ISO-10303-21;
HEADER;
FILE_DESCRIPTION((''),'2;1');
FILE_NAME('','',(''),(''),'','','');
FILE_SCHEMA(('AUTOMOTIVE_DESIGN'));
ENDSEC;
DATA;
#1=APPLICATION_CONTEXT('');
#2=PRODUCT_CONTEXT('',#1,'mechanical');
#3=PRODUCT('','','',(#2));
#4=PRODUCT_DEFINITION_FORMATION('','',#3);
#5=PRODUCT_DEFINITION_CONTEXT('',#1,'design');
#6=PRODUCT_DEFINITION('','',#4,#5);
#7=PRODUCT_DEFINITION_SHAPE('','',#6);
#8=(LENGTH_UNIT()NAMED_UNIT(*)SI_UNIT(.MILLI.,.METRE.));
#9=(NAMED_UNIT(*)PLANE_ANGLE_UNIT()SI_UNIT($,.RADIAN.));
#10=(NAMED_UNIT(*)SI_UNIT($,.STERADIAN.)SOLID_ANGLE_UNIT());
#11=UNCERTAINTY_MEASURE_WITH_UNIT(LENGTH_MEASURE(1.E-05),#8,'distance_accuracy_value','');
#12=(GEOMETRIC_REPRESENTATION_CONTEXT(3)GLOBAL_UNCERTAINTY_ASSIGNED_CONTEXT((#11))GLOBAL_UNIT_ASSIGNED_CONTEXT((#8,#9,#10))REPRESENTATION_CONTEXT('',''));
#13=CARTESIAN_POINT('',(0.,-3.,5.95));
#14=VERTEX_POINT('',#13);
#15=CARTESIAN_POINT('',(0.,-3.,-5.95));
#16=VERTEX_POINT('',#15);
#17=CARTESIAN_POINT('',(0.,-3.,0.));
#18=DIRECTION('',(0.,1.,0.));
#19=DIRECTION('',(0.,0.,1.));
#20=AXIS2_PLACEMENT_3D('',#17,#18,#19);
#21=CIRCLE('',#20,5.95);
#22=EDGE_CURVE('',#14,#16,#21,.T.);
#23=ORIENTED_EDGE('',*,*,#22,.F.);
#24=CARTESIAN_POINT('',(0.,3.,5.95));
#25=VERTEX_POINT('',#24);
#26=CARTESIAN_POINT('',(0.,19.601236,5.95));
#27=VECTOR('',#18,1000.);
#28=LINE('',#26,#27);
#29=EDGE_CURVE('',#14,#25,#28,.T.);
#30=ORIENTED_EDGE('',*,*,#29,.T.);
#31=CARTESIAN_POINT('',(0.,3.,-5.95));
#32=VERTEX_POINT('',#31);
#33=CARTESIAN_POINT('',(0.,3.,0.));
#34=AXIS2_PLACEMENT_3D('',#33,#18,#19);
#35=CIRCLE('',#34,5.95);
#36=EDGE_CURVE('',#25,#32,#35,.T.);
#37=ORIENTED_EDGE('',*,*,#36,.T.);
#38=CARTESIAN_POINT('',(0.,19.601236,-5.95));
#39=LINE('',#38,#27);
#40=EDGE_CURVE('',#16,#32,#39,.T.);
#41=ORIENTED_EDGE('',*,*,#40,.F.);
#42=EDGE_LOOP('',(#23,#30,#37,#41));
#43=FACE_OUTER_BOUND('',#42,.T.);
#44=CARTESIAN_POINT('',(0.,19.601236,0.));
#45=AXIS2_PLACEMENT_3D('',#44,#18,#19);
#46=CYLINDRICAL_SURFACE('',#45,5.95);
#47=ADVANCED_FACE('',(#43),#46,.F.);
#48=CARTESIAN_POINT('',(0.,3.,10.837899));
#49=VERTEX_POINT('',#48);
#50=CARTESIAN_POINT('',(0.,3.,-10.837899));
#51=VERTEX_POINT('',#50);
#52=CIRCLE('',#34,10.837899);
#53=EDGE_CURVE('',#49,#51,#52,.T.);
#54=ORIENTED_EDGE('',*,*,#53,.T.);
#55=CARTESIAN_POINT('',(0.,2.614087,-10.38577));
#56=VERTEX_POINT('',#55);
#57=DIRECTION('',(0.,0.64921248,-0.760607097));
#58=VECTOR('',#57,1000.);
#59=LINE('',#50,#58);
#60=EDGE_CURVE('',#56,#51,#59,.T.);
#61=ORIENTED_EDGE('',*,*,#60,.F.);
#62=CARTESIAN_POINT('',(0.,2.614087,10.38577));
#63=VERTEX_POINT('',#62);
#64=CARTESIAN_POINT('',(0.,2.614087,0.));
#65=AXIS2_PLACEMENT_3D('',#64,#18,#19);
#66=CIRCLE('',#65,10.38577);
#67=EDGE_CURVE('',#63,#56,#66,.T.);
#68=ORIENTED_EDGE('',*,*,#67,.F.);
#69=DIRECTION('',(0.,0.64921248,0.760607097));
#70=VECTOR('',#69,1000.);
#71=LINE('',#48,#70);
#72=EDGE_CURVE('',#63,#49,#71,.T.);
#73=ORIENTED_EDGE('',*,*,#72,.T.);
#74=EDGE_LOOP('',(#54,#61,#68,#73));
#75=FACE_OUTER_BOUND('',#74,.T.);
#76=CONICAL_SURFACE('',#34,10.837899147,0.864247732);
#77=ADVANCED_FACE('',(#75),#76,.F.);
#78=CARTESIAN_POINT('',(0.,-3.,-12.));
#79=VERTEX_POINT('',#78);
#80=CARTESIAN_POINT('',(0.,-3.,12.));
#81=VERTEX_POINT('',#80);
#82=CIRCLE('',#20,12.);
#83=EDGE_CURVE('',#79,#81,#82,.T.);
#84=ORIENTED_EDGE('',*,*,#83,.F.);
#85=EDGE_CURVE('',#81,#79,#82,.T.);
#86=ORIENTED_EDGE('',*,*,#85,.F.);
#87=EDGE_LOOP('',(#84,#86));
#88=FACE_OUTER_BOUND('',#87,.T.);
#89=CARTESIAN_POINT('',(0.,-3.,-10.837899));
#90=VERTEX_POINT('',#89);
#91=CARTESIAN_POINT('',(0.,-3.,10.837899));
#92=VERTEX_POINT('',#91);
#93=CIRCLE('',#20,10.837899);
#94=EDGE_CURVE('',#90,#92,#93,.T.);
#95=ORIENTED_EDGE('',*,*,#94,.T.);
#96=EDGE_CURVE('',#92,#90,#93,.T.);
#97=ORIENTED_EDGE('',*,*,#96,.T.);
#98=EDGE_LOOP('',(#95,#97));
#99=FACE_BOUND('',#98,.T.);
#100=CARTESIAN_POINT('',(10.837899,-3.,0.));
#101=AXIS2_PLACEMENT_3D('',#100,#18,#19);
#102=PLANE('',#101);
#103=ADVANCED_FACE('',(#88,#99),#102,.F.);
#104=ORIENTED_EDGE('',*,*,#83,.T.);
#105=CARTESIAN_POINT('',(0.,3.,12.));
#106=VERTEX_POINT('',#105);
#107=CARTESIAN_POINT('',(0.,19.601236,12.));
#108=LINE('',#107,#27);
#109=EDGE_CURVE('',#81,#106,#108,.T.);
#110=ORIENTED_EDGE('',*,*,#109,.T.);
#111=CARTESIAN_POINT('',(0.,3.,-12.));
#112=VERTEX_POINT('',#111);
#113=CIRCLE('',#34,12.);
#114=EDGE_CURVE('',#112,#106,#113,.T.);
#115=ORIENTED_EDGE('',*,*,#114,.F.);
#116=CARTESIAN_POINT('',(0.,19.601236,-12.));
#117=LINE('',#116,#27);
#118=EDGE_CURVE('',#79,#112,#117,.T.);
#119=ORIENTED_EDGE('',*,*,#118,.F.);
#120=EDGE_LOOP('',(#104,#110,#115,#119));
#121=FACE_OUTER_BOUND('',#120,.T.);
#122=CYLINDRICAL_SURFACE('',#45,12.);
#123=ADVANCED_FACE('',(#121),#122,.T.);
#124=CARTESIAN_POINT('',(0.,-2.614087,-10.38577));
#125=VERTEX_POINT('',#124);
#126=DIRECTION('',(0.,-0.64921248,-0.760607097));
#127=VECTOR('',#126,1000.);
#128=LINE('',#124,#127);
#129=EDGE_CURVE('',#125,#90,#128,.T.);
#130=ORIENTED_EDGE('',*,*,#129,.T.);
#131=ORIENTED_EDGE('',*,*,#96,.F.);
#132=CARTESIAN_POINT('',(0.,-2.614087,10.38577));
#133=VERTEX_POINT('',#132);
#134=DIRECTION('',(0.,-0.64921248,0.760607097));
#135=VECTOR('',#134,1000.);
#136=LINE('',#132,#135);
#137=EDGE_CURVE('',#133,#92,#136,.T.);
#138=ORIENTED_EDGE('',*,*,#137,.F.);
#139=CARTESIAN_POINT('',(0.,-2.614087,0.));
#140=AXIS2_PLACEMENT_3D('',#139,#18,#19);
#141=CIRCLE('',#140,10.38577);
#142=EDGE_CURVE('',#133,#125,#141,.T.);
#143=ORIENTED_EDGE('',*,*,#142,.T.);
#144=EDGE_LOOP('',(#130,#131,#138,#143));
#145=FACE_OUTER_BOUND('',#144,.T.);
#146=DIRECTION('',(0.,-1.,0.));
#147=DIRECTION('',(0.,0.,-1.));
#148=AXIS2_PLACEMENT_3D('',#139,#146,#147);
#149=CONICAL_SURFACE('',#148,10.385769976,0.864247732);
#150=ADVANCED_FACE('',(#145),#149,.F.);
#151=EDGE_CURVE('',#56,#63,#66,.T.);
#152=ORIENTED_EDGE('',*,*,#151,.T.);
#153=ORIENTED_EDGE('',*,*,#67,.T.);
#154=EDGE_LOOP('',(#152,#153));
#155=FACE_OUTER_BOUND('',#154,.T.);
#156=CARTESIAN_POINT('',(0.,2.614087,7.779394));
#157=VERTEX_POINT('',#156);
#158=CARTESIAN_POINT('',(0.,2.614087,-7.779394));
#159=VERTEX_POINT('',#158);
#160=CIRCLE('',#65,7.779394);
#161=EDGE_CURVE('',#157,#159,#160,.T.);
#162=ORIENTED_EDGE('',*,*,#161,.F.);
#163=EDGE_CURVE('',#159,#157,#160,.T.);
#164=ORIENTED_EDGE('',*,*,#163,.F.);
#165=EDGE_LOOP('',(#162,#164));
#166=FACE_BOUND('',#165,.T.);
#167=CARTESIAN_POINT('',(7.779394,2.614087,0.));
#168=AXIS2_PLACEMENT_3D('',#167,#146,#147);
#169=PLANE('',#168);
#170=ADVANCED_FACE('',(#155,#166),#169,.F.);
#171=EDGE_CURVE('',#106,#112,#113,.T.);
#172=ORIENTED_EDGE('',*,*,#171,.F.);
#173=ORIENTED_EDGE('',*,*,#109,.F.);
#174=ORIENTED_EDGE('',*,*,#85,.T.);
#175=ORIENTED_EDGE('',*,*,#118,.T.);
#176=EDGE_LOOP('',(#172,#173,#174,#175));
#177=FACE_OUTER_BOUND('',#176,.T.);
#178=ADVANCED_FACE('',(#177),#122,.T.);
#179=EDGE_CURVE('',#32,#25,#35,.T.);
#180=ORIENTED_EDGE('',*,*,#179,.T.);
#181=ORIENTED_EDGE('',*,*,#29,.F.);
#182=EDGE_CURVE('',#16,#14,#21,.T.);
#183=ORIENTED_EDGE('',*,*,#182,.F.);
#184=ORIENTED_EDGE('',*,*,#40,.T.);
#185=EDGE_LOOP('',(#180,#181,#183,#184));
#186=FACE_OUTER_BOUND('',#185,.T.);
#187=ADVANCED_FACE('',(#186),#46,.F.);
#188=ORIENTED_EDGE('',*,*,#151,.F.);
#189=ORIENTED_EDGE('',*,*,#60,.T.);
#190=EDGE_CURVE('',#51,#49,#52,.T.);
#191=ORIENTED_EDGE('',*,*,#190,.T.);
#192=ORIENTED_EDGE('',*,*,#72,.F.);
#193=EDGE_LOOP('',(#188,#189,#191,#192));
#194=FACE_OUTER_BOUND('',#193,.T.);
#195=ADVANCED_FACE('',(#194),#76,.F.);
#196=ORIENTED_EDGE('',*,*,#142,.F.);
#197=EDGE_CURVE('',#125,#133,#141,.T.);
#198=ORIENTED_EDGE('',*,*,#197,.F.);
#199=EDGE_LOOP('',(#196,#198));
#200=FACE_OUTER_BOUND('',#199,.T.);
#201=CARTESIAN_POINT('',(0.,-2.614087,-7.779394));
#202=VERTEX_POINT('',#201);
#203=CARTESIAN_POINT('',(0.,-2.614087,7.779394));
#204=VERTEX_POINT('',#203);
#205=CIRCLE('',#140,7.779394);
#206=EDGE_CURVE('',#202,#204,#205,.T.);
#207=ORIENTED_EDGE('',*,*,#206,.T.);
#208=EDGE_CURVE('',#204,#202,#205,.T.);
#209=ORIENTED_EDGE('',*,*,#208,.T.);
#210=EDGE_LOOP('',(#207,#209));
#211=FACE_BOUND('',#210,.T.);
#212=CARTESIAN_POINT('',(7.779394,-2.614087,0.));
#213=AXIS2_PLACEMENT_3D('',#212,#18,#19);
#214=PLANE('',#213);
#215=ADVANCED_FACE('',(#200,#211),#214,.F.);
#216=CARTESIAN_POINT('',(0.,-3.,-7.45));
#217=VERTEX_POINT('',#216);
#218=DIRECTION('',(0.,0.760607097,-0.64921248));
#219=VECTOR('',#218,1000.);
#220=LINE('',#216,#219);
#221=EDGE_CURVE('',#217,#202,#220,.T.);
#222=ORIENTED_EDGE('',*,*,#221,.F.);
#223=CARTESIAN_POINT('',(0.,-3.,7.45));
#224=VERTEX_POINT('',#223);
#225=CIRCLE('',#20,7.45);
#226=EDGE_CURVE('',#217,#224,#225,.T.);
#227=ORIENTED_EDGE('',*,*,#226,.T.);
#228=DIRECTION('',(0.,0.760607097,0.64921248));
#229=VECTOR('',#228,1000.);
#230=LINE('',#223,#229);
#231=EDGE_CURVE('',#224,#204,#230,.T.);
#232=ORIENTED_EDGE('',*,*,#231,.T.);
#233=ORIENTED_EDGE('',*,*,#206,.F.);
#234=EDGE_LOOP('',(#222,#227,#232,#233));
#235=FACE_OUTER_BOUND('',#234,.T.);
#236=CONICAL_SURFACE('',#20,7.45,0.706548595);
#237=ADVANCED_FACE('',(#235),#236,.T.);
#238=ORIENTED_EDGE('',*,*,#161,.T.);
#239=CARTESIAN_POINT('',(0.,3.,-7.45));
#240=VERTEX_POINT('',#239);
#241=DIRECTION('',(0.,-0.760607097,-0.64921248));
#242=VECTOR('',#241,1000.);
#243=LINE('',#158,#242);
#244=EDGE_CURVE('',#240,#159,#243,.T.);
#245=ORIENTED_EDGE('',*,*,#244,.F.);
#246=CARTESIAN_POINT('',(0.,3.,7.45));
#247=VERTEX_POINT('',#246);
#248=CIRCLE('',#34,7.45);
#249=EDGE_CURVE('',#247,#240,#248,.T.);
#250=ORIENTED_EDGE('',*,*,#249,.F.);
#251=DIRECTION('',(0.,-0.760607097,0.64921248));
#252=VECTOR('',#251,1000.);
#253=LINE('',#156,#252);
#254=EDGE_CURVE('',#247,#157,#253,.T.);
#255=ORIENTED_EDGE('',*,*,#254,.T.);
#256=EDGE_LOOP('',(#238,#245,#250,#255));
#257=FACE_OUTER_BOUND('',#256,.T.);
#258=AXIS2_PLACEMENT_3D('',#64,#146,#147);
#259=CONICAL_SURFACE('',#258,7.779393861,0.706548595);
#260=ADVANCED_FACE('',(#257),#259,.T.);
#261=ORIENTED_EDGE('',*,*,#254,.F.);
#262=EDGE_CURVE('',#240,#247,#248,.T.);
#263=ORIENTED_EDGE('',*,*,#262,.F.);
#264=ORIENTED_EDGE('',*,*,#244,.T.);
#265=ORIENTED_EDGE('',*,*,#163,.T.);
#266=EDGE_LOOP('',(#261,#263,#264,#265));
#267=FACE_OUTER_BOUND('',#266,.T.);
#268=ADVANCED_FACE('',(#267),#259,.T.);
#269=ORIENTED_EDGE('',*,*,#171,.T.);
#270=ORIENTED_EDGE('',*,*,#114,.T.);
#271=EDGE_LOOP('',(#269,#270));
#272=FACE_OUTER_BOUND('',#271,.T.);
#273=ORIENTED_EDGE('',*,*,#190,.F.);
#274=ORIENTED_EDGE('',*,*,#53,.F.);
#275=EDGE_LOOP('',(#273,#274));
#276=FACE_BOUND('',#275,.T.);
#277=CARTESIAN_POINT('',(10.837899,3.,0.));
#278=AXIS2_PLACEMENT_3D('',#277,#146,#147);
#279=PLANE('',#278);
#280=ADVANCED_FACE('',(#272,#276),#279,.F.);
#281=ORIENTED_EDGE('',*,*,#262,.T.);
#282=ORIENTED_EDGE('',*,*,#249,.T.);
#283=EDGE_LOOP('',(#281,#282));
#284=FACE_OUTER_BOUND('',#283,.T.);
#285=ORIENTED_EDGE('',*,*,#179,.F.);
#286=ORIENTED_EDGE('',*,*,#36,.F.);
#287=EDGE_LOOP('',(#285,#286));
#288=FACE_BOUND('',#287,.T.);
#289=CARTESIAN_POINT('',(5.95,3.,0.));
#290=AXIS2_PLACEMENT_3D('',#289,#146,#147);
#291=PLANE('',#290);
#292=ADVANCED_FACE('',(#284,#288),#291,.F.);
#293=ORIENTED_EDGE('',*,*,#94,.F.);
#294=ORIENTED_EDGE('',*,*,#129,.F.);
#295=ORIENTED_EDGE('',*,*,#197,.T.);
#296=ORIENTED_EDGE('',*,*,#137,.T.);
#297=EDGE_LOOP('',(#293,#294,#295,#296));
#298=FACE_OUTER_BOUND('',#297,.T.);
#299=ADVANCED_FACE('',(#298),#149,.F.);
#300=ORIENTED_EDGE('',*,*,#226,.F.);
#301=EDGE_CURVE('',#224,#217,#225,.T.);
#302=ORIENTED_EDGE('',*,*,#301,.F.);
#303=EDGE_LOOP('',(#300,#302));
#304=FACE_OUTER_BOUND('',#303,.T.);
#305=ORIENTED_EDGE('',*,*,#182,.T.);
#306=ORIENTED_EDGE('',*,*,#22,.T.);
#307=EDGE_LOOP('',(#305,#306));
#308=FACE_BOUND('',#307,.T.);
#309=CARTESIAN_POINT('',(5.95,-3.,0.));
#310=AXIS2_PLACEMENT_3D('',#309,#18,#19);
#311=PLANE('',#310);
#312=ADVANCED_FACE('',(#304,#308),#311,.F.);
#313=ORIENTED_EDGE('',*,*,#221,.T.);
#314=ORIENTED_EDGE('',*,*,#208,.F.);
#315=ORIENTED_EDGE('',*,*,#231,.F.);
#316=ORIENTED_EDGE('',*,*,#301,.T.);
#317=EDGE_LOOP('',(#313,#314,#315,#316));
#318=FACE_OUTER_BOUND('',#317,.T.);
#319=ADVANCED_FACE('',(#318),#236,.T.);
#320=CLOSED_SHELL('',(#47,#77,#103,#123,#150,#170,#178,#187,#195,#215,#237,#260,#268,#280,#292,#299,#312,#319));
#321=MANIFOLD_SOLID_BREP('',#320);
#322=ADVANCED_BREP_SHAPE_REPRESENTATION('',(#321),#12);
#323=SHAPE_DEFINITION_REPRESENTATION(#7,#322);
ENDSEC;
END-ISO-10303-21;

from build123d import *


with BuildPart() as part:
    # 草图1 → 旋转1 (revolve)
    with BuildSketch(Plane.XY, mode=Mode.PRIVATE) as revolve_1_sk:
        Polygon((5.95, 3), (5.95, -3), (7.45, -3), (7.779393861, -2.61408735), (10.385769976, -2.61408735), (10.837899147, -3), (12, -3), (12, 3), (10.837899147, 3), (10.385769976, 2.61408735), (7.779393861, 2.61408735), (7.45, 3), align=None)
    revolve(revolve_1_sk.sketch.rotate(Axis((0, 19.601235698, 0), (0, -1, 0)), 90), axis=Axis((0, 19.601235698, 0), (0, -1, 0)))


solid = part.part
